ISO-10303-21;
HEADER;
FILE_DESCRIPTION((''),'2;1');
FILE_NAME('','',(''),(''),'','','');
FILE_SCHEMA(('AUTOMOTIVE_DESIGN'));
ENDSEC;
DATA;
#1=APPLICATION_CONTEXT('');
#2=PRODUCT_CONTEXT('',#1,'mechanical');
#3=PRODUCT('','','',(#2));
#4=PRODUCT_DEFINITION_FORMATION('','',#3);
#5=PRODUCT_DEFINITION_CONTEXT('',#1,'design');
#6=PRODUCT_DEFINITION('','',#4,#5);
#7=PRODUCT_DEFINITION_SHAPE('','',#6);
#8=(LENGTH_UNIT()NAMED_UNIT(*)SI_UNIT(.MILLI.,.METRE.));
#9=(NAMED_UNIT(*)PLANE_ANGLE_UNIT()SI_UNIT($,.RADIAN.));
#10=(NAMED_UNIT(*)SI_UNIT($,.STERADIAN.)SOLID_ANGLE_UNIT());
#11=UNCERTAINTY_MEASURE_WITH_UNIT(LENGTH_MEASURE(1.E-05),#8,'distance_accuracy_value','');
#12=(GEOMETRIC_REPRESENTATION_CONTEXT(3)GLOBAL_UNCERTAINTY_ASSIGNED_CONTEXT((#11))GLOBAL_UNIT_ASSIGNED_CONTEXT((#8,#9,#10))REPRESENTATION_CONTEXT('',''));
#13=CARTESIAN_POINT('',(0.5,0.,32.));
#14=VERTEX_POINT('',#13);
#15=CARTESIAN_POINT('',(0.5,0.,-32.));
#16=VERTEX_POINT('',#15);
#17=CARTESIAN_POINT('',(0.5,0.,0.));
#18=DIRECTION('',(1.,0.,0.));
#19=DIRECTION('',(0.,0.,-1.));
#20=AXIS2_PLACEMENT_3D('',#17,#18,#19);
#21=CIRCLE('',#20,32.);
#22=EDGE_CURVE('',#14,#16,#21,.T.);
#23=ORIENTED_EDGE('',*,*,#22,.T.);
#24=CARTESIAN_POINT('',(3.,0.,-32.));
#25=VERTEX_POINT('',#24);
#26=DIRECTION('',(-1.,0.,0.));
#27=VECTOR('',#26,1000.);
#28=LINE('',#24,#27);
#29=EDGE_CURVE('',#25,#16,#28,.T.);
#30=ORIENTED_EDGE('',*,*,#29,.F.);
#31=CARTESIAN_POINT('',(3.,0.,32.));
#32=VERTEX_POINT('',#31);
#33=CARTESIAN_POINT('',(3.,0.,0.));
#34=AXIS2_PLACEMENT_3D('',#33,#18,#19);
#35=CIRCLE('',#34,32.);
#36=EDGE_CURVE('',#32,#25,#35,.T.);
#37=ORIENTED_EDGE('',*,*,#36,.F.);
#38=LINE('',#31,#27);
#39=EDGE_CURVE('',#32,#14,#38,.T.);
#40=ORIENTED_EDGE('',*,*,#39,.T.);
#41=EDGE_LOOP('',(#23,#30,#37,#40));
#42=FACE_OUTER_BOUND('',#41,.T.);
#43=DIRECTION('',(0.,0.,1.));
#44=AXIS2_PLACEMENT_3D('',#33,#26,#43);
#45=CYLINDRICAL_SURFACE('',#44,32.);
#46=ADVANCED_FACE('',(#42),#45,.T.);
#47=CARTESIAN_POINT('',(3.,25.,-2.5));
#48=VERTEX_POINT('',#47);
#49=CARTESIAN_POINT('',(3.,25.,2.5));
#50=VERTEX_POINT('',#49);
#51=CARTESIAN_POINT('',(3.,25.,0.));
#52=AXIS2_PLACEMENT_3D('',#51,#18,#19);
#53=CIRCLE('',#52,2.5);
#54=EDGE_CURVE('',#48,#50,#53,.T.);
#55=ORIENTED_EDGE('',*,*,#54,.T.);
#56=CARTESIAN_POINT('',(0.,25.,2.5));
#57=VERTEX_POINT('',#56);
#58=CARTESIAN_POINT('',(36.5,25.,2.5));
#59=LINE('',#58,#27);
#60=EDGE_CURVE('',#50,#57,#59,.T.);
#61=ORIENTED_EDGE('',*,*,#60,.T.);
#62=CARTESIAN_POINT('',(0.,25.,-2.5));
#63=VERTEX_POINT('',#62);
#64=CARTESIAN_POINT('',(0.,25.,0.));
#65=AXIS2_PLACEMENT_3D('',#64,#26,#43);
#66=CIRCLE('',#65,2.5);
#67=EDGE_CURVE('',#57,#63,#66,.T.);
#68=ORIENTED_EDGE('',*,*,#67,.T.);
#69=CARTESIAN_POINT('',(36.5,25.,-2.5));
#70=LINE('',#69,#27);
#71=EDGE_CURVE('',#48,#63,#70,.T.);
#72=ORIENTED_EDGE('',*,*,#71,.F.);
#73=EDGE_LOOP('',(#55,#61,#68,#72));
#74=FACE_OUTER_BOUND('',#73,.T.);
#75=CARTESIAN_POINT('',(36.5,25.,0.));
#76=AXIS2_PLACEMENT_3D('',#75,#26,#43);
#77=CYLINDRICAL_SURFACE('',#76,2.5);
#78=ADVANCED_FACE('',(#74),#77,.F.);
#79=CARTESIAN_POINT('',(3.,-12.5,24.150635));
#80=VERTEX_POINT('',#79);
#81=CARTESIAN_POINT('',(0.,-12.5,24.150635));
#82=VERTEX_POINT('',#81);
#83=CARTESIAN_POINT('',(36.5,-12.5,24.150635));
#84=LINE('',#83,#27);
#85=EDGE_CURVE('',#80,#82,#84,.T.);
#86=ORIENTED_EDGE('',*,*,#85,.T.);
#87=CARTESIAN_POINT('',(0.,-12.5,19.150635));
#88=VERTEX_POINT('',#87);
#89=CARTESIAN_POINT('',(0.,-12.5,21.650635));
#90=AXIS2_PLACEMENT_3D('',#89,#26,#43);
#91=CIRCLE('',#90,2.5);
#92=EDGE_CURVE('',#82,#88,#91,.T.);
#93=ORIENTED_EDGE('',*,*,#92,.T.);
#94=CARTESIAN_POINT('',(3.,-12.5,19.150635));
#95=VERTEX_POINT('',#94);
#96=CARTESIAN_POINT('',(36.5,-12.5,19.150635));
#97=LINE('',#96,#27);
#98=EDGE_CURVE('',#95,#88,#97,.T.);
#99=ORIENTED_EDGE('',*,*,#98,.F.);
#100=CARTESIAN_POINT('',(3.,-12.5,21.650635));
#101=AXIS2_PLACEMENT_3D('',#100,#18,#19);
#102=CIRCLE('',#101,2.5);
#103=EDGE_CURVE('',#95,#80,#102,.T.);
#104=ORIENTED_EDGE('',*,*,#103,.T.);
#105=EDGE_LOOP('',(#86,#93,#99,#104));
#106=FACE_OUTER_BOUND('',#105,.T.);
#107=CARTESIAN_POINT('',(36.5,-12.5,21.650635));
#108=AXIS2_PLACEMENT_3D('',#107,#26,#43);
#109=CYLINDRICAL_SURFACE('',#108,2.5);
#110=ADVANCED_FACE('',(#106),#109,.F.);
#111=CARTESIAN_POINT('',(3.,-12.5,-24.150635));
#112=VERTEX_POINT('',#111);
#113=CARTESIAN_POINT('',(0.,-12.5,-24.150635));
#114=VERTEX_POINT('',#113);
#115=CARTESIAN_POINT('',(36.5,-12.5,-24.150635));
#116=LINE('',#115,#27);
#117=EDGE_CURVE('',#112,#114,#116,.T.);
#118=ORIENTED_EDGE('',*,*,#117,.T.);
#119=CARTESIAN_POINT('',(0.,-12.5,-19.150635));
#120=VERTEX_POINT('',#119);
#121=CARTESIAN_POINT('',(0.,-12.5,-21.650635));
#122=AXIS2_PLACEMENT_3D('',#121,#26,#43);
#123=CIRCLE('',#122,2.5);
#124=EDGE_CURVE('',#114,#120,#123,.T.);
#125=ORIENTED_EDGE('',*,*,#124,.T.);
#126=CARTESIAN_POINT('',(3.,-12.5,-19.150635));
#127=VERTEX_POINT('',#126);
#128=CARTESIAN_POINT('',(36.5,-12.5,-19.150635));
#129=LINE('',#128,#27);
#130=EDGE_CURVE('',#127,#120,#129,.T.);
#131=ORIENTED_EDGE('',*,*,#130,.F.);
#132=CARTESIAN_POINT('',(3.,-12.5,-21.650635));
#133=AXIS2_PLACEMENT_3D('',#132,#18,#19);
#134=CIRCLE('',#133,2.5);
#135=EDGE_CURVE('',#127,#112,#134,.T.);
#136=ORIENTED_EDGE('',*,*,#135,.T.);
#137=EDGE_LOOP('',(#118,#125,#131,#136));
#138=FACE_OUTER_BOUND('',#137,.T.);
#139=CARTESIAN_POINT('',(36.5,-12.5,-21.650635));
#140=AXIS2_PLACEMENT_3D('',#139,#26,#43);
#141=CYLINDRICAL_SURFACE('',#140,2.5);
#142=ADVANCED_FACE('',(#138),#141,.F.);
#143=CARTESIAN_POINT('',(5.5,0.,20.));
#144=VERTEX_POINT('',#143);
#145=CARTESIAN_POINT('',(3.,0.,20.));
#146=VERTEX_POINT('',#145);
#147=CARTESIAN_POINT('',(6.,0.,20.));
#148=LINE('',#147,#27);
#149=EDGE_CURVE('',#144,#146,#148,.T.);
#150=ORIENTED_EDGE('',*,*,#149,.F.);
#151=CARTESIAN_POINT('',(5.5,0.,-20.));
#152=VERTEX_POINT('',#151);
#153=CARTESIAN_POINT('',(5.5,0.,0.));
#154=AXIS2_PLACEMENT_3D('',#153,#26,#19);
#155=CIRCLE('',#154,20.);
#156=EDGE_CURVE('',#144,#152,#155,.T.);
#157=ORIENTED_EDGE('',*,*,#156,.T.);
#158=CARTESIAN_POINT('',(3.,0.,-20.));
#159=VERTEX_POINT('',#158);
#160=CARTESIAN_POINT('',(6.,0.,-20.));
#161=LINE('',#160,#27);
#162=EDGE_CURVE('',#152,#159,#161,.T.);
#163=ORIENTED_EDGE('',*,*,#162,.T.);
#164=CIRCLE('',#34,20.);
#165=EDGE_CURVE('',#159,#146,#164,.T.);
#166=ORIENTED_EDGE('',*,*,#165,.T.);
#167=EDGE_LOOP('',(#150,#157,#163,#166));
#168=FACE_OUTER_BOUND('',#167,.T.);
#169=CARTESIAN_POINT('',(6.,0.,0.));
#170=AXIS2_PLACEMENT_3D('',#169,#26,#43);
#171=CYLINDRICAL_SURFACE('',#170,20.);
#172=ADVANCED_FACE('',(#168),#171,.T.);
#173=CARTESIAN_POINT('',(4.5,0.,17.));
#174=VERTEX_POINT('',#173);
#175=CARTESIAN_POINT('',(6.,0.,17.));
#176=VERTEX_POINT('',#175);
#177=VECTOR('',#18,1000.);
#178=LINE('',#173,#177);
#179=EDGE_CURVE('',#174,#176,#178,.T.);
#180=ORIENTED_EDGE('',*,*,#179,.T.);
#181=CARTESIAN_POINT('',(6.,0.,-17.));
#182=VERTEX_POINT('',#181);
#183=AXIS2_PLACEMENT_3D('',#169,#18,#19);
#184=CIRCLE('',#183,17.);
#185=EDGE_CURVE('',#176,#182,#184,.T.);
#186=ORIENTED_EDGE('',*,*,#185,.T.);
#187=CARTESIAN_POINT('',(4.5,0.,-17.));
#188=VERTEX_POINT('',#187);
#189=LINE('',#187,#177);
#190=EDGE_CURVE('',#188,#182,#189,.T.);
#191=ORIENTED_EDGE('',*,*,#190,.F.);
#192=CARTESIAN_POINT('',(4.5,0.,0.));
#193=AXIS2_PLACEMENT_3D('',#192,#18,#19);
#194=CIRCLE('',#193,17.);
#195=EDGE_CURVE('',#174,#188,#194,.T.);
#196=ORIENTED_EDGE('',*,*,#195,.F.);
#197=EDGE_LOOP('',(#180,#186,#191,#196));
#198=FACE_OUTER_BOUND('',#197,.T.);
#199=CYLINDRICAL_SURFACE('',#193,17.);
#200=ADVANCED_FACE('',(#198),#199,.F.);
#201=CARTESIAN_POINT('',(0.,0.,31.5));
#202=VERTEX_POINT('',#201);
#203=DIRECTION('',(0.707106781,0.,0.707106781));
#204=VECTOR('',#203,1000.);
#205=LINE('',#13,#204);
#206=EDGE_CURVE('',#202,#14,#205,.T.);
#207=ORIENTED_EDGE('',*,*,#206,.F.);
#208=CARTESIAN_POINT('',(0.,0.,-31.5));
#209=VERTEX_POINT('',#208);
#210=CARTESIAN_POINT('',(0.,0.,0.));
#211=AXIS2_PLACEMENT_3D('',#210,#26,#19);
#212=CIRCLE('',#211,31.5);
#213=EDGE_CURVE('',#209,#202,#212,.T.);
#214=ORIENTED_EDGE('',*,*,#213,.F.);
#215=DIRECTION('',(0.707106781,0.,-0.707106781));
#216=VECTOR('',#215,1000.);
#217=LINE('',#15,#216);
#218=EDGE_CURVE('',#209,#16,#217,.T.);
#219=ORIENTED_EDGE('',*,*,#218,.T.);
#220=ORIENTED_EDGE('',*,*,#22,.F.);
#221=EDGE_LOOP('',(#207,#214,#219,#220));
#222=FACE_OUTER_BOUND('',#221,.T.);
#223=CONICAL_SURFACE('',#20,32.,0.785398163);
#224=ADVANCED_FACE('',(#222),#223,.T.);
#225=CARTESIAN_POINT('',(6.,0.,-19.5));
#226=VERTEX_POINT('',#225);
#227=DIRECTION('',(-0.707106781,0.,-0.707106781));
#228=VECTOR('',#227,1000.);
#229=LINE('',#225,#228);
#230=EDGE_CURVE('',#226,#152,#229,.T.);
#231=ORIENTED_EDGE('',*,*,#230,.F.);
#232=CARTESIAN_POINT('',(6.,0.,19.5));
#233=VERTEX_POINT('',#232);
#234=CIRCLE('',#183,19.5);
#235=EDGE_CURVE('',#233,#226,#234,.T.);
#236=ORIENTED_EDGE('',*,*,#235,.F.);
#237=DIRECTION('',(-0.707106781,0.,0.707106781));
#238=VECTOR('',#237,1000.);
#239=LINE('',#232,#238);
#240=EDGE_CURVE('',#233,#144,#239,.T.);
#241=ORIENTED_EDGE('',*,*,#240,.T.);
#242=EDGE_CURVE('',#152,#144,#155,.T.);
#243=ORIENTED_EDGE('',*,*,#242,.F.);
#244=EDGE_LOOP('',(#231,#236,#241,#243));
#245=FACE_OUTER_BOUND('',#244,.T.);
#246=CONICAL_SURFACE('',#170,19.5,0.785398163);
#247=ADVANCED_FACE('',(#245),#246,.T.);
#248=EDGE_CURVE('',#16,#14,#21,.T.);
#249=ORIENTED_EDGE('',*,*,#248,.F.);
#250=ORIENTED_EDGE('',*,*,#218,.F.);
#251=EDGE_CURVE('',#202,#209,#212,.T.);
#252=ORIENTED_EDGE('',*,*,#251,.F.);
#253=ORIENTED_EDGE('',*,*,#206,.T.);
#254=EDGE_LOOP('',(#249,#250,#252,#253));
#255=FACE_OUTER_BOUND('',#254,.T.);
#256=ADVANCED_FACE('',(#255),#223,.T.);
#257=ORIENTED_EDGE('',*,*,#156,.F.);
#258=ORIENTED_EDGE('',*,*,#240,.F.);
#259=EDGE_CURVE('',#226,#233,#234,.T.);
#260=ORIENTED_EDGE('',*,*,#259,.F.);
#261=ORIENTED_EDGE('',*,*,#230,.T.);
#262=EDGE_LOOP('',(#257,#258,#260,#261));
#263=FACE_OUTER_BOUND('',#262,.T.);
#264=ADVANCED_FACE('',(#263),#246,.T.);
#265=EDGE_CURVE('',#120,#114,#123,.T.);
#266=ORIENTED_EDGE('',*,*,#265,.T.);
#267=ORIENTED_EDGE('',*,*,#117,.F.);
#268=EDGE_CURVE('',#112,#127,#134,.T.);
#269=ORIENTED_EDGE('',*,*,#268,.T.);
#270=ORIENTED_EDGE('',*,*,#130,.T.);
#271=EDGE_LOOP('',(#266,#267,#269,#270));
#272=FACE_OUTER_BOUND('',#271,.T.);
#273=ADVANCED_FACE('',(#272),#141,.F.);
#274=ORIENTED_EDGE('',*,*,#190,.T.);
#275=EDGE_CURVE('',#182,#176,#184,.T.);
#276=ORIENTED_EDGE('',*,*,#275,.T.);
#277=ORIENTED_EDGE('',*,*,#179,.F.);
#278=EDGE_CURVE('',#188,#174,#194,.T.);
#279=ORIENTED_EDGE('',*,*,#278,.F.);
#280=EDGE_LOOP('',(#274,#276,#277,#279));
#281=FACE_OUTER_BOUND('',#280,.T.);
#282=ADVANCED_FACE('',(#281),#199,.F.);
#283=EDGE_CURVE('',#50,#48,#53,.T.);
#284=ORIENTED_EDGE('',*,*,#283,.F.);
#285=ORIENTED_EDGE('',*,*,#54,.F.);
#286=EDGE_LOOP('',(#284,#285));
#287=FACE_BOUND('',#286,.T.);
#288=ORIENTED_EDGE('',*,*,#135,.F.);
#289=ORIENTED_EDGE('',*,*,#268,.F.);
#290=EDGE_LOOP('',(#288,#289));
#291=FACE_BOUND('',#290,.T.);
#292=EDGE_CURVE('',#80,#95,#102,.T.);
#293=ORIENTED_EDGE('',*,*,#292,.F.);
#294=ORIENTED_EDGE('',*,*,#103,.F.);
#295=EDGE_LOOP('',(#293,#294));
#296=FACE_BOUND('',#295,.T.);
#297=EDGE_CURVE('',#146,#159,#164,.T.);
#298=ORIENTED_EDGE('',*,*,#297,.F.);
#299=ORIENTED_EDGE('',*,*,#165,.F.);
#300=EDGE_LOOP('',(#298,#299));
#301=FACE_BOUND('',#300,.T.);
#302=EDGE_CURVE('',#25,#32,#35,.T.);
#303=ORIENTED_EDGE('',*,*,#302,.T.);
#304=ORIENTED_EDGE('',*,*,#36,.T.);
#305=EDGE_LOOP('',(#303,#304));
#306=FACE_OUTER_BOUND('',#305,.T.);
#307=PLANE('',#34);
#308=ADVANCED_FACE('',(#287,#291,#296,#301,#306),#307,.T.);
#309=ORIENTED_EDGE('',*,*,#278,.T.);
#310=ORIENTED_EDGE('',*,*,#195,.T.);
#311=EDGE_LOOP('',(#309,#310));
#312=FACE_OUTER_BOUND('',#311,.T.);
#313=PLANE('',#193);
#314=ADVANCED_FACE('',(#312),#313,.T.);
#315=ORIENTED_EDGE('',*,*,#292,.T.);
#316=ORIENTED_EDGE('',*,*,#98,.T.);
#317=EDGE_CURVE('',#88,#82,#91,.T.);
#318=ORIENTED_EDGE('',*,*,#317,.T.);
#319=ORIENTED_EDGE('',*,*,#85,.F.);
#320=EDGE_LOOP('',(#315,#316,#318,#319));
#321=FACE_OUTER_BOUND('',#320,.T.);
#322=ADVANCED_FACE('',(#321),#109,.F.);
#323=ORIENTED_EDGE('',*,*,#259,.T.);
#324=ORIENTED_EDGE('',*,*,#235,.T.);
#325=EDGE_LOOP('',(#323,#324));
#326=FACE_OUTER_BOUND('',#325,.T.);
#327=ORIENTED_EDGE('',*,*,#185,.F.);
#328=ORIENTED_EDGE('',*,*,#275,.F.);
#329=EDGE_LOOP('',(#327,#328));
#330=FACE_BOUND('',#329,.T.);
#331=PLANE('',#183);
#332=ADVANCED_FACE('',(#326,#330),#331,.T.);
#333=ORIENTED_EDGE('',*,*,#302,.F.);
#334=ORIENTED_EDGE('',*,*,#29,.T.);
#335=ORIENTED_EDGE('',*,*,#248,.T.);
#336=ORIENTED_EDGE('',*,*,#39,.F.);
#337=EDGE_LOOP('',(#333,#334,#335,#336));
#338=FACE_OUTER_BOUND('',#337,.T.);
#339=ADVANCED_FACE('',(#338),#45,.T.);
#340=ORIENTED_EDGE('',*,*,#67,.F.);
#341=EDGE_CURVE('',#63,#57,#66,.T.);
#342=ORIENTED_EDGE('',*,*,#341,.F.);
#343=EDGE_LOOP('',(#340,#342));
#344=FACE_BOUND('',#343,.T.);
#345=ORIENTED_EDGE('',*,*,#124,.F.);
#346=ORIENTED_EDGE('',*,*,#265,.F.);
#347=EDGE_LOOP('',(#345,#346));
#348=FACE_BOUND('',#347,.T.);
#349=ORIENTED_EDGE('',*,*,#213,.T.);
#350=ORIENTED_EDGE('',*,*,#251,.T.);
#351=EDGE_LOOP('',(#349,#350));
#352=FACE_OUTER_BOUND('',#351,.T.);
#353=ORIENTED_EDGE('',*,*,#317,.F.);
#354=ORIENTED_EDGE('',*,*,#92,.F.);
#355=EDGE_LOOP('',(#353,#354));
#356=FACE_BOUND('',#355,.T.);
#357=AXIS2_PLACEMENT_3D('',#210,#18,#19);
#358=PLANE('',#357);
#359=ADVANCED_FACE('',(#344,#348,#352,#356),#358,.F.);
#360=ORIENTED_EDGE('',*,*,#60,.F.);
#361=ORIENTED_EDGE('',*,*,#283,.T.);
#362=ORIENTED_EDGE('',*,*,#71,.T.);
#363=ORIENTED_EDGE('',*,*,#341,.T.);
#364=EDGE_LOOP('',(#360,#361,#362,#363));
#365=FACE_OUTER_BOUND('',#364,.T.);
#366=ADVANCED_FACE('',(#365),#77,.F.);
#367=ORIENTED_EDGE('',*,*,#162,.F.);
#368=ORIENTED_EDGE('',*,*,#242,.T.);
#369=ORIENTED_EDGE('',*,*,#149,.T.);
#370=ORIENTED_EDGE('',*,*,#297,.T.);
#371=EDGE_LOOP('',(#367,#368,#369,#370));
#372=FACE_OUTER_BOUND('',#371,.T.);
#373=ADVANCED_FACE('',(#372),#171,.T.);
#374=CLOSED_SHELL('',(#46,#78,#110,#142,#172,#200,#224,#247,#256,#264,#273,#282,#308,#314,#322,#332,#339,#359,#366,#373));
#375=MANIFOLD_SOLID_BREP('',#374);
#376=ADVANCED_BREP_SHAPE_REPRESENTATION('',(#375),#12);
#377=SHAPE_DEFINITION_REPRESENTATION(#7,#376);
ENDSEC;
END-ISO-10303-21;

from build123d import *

# Parameters (mm, degrees)
SKETCH1_R           = 32
BOSS_EXTRUDE1_DEPTH = 3
SKETCH2_R           = 20
BOSS_EXTRUDE2_DEPTH = 3
SKETCH3_R           = 17
CUT_EXTRUDE1_DEPTH  = 1.5
SKETCH4_R           = 2.5
CUT_EXTRUDE2_DEPTH  = 36.5
CHAMFER1_SIZE       = 0.5


with BuildPart() as part:
    # Sketch1 → Boss-Extrude1 (new body)
    with BuildSketch(Plane(origin=(0, 0, 0), x_dir=(0, 0, -1), z_dir=(1, 0, 0))):
        Circle(SKETCH1_R)
    extrude(amount=BOSS_EXTRUDE1_DEPTH)

    # Sketch2 → Boss-Extrude2 (add)
    with BuildSketch(Plane(origin=(3, 0, 0), x_dir=(0, 0, -1), z_dir=(1, 0, 0))):
        Circle(SKETCH2_R)
    extrude(amount=BOSS_EXTRUDE2_DEPTH)

    # Sketch3 → Cut-Extrude1 (cut)
    with BuildSketch(Plane(origin=(6, 0, 0), x_dir=(0, 0, -1), z_dir=(1, 0, 0))):
        Circle(SKETCH3_R)
    extrude(amount=-CUT_EXTRUDE1_DEPTH, mode=Mode.SUBTRACT)

    # Sketch4 → Cut-Extrude2 (cut)
    with BuildSketch(Plane.ZY):
        with Locations((0, 25)):
            Circle(SKETCH4_R)
        with Locations((21.650635095, -12.5)):
            Circle(SKETCH4_R)
        with Locations((-21.650635095, -12.5)):
            Circle(SKETCH4_R)
    extrude(amount=-CUT_EXTRUDE2_DEPTH, mode=Mode.SUBTRACT)

    # Chamfer1
    chamfer1_edges = [part.edges().sort_by_distance(p)[0] for p in [
        (0, 0, 32),
        (6, 0, 20),
    ]]
    chamfer(chamfer1_edges, length=CHAMFER1_SIZE)


solid = part.part
